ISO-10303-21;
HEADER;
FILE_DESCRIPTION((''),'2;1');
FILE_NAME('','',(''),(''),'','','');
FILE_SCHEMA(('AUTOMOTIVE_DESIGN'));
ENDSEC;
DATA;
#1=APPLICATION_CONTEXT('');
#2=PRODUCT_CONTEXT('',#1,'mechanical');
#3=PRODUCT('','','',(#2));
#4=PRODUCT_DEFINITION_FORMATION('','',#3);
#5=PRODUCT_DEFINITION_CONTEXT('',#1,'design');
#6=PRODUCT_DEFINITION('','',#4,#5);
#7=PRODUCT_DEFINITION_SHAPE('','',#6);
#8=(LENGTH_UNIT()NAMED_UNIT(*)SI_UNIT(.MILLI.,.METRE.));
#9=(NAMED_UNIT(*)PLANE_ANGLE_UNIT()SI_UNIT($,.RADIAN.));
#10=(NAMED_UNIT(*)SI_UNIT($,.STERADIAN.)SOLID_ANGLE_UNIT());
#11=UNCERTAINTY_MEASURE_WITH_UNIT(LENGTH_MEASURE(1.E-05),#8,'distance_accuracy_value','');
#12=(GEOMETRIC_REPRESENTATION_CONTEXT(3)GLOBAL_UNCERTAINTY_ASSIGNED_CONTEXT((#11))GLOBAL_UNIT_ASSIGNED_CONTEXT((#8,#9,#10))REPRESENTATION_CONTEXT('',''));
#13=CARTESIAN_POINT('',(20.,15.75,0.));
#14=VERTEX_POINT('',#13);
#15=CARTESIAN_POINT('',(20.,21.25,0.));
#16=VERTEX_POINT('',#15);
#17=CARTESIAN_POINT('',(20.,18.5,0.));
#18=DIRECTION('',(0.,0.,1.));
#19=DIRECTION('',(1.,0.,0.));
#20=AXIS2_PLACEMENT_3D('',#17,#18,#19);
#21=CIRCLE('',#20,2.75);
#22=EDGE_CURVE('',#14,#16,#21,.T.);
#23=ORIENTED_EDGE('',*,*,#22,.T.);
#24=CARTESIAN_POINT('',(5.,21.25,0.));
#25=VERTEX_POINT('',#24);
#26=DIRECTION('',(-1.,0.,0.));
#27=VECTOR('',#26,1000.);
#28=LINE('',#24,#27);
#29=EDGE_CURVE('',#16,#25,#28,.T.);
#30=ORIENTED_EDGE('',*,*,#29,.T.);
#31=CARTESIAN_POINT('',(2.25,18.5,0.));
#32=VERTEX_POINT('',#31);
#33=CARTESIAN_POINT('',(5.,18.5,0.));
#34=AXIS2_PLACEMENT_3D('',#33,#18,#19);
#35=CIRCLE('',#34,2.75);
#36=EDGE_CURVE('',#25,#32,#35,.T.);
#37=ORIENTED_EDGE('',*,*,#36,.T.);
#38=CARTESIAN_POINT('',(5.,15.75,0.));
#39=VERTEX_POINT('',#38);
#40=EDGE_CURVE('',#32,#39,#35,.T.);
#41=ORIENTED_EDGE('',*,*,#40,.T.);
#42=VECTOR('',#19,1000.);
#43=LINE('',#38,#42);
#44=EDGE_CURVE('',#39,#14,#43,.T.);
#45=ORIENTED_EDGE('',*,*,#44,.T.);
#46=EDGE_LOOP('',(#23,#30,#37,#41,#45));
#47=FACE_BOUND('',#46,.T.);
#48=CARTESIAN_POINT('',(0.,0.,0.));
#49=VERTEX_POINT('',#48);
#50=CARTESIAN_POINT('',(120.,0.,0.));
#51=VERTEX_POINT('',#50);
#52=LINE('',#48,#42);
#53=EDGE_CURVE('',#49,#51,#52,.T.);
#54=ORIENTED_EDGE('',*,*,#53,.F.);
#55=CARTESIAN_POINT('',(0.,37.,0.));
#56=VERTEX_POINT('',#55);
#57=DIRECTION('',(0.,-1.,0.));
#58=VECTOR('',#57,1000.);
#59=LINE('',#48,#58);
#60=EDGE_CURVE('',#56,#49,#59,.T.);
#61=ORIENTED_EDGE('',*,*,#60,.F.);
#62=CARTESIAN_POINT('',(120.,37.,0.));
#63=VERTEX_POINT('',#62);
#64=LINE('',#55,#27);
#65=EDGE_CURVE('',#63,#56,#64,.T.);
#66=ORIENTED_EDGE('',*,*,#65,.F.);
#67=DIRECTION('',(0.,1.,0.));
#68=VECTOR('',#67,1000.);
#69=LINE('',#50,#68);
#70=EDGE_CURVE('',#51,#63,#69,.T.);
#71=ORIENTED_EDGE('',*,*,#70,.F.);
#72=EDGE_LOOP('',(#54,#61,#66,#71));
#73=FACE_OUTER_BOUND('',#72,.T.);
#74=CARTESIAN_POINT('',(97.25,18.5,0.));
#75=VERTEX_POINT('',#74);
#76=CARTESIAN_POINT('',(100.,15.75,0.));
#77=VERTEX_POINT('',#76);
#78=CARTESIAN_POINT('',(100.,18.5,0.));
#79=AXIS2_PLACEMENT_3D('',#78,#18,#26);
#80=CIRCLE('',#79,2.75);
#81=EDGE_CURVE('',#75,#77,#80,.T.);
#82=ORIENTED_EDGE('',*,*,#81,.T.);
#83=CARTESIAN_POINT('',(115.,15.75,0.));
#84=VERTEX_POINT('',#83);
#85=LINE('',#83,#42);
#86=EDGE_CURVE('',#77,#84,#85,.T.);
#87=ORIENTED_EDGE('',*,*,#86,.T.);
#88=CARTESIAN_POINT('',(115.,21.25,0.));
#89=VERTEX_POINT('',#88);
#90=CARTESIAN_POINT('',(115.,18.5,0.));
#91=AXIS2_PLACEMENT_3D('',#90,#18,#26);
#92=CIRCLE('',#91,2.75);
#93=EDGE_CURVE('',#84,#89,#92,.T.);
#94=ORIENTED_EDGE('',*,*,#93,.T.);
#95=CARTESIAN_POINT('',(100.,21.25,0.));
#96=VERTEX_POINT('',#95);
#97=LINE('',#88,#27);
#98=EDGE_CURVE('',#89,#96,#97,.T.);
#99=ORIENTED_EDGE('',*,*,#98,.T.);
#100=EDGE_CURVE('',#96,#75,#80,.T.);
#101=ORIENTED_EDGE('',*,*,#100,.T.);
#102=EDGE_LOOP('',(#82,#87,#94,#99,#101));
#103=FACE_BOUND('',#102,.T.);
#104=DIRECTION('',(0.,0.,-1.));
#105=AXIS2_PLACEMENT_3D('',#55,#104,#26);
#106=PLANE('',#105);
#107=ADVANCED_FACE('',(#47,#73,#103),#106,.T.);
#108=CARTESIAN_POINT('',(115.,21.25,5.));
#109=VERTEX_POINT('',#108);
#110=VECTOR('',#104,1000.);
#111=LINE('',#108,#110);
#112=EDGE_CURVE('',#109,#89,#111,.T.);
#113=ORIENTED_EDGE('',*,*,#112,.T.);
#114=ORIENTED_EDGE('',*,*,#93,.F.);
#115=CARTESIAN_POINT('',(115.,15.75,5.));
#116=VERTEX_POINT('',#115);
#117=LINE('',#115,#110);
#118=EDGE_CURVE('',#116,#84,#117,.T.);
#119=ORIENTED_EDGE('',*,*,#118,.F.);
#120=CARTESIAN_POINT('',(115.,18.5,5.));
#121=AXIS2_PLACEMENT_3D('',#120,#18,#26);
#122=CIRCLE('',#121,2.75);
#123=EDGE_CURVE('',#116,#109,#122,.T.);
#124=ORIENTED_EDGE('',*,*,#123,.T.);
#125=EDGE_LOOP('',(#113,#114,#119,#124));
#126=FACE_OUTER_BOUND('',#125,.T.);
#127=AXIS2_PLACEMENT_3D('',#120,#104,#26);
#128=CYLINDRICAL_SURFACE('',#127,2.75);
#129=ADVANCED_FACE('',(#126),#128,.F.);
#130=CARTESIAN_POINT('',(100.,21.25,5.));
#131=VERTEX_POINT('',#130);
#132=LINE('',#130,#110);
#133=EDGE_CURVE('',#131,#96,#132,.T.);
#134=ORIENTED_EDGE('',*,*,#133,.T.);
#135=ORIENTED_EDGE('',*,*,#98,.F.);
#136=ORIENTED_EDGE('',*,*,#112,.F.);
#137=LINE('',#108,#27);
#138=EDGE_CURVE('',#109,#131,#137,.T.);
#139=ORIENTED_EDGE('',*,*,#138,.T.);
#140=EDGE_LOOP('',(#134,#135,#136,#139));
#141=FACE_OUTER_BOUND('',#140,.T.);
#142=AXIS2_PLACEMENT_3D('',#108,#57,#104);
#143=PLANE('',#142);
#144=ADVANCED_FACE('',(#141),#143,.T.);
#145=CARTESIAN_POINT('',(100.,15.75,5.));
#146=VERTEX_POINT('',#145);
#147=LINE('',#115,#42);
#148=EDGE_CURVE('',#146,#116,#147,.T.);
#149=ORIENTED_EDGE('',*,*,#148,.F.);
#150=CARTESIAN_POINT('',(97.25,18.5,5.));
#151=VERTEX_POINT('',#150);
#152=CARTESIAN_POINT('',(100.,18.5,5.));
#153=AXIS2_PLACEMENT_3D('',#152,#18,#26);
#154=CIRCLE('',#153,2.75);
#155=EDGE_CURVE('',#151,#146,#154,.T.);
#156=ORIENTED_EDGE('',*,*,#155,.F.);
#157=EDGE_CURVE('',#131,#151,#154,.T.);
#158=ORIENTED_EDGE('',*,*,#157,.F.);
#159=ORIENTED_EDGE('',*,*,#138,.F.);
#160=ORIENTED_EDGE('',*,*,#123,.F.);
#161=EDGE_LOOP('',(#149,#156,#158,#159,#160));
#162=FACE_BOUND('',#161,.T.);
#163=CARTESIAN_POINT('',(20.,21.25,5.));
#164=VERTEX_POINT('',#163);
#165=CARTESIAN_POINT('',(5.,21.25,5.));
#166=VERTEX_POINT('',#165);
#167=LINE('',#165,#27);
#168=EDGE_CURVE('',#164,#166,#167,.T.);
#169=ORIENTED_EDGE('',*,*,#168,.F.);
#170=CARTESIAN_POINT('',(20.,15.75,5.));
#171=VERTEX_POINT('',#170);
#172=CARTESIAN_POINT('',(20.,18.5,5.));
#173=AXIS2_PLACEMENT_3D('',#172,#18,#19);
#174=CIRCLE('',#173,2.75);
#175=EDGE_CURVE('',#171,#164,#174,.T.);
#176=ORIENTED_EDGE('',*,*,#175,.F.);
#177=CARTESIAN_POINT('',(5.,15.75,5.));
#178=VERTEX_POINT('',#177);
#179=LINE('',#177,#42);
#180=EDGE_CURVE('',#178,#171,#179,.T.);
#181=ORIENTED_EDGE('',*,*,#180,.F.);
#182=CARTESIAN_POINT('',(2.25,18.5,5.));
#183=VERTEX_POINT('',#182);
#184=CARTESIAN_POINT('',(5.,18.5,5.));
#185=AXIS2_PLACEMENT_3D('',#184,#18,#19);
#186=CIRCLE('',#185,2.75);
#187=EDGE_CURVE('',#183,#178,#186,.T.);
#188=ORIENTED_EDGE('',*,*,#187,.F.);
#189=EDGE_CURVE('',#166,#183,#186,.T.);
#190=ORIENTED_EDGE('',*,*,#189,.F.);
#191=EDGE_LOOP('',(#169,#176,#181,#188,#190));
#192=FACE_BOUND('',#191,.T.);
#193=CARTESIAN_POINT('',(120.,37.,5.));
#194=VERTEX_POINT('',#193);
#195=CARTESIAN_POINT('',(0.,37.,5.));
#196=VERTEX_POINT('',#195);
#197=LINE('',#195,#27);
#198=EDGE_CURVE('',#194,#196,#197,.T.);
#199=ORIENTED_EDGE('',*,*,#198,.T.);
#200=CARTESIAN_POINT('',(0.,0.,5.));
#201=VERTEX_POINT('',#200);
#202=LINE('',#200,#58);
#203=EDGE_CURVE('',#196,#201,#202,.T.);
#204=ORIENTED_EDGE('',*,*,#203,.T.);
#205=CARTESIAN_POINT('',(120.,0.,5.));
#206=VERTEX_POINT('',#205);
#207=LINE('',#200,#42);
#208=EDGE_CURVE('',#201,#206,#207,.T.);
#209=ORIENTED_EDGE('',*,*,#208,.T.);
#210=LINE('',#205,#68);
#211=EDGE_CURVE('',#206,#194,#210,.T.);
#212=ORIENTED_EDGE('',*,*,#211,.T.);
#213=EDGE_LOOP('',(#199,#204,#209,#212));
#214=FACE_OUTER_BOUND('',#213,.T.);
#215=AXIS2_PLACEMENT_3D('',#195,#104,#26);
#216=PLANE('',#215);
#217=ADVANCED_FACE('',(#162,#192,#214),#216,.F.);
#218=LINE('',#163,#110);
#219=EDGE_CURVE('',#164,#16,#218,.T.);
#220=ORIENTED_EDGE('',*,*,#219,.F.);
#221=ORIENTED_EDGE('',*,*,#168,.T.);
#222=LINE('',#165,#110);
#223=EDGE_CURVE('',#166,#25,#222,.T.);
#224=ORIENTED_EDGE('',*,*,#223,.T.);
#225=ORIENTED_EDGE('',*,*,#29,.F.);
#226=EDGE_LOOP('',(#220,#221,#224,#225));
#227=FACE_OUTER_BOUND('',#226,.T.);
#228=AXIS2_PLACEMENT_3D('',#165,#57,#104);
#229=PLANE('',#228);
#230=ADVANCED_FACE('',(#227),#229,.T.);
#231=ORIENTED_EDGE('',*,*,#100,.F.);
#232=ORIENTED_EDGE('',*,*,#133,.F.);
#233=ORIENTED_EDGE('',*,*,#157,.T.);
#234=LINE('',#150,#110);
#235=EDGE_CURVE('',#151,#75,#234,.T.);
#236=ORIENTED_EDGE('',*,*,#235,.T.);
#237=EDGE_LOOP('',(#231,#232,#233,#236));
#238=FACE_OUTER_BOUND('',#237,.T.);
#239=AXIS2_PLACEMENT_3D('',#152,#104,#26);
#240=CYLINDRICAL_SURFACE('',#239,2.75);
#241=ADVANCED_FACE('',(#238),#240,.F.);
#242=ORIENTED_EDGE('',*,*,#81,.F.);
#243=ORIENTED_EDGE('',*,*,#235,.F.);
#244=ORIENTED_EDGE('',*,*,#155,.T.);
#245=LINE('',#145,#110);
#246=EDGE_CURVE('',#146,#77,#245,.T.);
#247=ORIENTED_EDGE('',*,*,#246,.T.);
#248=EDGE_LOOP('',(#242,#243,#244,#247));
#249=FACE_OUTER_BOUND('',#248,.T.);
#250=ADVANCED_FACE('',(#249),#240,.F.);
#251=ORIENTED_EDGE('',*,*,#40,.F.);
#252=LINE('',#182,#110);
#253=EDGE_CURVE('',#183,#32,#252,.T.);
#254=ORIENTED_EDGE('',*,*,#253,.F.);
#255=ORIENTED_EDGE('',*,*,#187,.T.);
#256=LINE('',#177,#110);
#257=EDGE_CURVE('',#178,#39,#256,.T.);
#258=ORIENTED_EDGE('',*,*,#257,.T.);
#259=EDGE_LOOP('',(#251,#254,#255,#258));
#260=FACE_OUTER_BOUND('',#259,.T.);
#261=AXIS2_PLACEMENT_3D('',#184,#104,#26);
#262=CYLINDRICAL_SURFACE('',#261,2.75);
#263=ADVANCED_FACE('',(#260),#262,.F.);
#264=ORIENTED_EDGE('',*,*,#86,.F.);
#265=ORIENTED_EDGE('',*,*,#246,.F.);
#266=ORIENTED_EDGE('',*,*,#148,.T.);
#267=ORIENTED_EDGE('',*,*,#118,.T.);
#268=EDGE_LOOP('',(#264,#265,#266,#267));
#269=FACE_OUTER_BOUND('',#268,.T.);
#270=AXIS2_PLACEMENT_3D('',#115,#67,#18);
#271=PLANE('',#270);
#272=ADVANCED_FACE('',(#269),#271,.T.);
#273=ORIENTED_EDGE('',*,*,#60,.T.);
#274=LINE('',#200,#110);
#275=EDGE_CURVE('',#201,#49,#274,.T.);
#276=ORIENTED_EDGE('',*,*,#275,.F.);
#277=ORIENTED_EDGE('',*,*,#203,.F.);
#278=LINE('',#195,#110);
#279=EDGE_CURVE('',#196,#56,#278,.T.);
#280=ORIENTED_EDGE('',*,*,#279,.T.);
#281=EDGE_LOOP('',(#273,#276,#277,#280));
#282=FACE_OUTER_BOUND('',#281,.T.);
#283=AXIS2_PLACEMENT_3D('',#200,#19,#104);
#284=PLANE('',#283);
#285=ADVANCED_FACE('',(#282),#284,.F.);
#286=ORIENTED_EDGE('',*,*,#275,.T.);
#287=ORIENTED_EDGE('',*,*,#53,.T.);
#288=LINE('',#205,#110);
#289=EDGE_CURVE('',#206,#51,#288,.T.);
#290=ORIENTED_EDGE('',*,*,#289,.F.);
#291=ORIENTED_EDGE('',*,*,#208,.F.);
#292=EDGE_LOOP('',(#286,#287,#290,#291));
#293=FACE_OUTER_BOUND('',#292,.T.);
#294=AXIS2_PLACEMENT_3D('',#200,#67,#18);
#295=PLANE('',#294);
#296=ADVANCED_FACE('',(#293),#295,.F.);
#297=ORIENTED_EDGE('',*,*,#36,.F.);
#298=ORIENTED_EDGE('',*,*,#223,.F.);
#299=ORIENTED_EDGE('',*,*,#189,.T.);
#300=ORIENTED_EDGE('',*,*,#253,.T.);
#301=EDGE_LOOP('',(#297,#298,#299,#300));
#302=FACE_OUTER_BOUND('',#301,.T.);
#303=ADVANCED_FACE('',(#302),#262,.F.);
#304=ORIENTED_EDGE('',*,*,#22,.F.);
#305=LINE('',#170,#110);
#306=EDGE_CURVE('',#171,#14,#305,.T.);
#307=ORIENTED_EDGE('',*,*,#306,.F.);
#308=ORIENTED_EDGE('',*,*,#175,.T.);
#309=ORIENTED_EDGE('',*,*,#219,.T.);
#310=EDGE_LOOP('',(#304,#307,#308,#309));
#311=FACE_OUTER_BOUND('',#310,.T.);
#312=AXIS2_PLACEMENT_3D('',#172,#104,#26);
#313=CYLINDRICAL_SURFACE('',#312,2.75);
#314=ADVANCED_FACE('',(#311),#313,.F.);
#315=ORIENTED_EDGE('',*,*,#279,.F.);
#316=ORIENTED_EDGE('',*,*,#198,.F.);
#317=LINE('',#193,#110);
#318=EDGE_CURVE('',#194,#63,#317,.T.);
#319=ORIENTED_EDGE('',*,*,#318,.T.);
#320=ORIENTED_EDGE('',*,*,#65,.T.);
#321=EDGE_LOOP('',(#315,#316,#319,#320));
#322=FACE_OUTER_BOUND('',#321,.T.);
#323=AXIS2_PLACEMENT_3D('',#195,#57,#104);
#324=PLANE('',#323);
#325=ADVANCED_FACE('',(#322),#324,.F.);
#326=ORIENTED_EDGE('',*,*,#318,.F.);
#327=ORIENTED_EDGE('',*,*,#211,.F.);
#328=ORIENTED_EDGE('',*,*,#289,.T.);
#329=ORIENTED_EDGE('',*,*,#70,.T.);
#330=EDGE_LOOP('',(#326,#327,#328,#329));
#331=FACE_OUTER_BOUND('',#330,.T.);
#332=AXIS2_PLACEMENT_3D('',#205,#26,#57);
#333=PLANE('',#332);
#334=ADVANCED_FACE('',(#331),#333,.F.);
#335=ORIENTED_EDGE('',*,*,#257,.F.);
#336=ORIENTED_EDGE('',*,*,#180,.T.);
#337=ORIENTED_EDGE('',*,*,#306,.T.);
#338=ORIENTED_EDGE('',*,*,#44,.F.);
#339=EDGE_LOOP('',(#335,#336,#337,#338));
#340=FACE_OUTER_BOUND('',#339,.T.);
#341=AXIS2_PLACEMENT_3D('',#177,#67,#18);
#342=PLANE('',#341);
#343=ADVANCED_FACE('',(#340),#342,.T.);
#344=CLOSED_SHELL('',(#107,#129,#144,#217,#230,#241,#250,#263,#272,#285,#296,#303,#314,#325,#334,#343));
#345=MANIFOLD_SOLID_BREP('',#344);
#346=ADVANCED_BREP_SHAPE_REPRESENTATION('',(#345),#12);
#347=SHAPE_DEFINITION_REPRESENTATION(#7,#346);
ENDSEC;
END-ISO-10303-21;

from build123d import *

# Parameters (mm, degrees)
SKETCH_1_W      = 120
SKETCH_1_H      = 37
EXTRUDE_1_DEPTH = 5


with BuildPart() as part:
    # 草图1 → 凸台-拉伸1 (new body)
    with BuildSketch(Plane.XY):
        with Locations((60, 18.5)):
            Rectangle(SKETCH_1_W, SKETCH_1_H)
        with BuildLine():
            Line((5, 21.25), (20, 21.25))
            ThreePointArc((20, 21.25), (22.75, 18.5), (20, 15.75))
            Line((20, 15.75), (5, 15.75))
            ThreePointArc((5, 15.75), (2.25, 18.5), (5, 21.25))
        make_face(mode=Mode.SUBTRACT)
        with BuildLine():
            Line((115, 15.75), (100, 15.75))
            ThreePointArc((100, 15.75), (97.25, 18.5), (100, 21.25))
            Line((100, 21.25), (115, 21.25))
            ThreePointArc((115, 21.25), (117.75, 18.5), (115, 15.75))
        make_face(mode=Mode.SUBTRACT)
    extrude(amount=EXTRUDE_1_DEPTH)


solid = part.part
